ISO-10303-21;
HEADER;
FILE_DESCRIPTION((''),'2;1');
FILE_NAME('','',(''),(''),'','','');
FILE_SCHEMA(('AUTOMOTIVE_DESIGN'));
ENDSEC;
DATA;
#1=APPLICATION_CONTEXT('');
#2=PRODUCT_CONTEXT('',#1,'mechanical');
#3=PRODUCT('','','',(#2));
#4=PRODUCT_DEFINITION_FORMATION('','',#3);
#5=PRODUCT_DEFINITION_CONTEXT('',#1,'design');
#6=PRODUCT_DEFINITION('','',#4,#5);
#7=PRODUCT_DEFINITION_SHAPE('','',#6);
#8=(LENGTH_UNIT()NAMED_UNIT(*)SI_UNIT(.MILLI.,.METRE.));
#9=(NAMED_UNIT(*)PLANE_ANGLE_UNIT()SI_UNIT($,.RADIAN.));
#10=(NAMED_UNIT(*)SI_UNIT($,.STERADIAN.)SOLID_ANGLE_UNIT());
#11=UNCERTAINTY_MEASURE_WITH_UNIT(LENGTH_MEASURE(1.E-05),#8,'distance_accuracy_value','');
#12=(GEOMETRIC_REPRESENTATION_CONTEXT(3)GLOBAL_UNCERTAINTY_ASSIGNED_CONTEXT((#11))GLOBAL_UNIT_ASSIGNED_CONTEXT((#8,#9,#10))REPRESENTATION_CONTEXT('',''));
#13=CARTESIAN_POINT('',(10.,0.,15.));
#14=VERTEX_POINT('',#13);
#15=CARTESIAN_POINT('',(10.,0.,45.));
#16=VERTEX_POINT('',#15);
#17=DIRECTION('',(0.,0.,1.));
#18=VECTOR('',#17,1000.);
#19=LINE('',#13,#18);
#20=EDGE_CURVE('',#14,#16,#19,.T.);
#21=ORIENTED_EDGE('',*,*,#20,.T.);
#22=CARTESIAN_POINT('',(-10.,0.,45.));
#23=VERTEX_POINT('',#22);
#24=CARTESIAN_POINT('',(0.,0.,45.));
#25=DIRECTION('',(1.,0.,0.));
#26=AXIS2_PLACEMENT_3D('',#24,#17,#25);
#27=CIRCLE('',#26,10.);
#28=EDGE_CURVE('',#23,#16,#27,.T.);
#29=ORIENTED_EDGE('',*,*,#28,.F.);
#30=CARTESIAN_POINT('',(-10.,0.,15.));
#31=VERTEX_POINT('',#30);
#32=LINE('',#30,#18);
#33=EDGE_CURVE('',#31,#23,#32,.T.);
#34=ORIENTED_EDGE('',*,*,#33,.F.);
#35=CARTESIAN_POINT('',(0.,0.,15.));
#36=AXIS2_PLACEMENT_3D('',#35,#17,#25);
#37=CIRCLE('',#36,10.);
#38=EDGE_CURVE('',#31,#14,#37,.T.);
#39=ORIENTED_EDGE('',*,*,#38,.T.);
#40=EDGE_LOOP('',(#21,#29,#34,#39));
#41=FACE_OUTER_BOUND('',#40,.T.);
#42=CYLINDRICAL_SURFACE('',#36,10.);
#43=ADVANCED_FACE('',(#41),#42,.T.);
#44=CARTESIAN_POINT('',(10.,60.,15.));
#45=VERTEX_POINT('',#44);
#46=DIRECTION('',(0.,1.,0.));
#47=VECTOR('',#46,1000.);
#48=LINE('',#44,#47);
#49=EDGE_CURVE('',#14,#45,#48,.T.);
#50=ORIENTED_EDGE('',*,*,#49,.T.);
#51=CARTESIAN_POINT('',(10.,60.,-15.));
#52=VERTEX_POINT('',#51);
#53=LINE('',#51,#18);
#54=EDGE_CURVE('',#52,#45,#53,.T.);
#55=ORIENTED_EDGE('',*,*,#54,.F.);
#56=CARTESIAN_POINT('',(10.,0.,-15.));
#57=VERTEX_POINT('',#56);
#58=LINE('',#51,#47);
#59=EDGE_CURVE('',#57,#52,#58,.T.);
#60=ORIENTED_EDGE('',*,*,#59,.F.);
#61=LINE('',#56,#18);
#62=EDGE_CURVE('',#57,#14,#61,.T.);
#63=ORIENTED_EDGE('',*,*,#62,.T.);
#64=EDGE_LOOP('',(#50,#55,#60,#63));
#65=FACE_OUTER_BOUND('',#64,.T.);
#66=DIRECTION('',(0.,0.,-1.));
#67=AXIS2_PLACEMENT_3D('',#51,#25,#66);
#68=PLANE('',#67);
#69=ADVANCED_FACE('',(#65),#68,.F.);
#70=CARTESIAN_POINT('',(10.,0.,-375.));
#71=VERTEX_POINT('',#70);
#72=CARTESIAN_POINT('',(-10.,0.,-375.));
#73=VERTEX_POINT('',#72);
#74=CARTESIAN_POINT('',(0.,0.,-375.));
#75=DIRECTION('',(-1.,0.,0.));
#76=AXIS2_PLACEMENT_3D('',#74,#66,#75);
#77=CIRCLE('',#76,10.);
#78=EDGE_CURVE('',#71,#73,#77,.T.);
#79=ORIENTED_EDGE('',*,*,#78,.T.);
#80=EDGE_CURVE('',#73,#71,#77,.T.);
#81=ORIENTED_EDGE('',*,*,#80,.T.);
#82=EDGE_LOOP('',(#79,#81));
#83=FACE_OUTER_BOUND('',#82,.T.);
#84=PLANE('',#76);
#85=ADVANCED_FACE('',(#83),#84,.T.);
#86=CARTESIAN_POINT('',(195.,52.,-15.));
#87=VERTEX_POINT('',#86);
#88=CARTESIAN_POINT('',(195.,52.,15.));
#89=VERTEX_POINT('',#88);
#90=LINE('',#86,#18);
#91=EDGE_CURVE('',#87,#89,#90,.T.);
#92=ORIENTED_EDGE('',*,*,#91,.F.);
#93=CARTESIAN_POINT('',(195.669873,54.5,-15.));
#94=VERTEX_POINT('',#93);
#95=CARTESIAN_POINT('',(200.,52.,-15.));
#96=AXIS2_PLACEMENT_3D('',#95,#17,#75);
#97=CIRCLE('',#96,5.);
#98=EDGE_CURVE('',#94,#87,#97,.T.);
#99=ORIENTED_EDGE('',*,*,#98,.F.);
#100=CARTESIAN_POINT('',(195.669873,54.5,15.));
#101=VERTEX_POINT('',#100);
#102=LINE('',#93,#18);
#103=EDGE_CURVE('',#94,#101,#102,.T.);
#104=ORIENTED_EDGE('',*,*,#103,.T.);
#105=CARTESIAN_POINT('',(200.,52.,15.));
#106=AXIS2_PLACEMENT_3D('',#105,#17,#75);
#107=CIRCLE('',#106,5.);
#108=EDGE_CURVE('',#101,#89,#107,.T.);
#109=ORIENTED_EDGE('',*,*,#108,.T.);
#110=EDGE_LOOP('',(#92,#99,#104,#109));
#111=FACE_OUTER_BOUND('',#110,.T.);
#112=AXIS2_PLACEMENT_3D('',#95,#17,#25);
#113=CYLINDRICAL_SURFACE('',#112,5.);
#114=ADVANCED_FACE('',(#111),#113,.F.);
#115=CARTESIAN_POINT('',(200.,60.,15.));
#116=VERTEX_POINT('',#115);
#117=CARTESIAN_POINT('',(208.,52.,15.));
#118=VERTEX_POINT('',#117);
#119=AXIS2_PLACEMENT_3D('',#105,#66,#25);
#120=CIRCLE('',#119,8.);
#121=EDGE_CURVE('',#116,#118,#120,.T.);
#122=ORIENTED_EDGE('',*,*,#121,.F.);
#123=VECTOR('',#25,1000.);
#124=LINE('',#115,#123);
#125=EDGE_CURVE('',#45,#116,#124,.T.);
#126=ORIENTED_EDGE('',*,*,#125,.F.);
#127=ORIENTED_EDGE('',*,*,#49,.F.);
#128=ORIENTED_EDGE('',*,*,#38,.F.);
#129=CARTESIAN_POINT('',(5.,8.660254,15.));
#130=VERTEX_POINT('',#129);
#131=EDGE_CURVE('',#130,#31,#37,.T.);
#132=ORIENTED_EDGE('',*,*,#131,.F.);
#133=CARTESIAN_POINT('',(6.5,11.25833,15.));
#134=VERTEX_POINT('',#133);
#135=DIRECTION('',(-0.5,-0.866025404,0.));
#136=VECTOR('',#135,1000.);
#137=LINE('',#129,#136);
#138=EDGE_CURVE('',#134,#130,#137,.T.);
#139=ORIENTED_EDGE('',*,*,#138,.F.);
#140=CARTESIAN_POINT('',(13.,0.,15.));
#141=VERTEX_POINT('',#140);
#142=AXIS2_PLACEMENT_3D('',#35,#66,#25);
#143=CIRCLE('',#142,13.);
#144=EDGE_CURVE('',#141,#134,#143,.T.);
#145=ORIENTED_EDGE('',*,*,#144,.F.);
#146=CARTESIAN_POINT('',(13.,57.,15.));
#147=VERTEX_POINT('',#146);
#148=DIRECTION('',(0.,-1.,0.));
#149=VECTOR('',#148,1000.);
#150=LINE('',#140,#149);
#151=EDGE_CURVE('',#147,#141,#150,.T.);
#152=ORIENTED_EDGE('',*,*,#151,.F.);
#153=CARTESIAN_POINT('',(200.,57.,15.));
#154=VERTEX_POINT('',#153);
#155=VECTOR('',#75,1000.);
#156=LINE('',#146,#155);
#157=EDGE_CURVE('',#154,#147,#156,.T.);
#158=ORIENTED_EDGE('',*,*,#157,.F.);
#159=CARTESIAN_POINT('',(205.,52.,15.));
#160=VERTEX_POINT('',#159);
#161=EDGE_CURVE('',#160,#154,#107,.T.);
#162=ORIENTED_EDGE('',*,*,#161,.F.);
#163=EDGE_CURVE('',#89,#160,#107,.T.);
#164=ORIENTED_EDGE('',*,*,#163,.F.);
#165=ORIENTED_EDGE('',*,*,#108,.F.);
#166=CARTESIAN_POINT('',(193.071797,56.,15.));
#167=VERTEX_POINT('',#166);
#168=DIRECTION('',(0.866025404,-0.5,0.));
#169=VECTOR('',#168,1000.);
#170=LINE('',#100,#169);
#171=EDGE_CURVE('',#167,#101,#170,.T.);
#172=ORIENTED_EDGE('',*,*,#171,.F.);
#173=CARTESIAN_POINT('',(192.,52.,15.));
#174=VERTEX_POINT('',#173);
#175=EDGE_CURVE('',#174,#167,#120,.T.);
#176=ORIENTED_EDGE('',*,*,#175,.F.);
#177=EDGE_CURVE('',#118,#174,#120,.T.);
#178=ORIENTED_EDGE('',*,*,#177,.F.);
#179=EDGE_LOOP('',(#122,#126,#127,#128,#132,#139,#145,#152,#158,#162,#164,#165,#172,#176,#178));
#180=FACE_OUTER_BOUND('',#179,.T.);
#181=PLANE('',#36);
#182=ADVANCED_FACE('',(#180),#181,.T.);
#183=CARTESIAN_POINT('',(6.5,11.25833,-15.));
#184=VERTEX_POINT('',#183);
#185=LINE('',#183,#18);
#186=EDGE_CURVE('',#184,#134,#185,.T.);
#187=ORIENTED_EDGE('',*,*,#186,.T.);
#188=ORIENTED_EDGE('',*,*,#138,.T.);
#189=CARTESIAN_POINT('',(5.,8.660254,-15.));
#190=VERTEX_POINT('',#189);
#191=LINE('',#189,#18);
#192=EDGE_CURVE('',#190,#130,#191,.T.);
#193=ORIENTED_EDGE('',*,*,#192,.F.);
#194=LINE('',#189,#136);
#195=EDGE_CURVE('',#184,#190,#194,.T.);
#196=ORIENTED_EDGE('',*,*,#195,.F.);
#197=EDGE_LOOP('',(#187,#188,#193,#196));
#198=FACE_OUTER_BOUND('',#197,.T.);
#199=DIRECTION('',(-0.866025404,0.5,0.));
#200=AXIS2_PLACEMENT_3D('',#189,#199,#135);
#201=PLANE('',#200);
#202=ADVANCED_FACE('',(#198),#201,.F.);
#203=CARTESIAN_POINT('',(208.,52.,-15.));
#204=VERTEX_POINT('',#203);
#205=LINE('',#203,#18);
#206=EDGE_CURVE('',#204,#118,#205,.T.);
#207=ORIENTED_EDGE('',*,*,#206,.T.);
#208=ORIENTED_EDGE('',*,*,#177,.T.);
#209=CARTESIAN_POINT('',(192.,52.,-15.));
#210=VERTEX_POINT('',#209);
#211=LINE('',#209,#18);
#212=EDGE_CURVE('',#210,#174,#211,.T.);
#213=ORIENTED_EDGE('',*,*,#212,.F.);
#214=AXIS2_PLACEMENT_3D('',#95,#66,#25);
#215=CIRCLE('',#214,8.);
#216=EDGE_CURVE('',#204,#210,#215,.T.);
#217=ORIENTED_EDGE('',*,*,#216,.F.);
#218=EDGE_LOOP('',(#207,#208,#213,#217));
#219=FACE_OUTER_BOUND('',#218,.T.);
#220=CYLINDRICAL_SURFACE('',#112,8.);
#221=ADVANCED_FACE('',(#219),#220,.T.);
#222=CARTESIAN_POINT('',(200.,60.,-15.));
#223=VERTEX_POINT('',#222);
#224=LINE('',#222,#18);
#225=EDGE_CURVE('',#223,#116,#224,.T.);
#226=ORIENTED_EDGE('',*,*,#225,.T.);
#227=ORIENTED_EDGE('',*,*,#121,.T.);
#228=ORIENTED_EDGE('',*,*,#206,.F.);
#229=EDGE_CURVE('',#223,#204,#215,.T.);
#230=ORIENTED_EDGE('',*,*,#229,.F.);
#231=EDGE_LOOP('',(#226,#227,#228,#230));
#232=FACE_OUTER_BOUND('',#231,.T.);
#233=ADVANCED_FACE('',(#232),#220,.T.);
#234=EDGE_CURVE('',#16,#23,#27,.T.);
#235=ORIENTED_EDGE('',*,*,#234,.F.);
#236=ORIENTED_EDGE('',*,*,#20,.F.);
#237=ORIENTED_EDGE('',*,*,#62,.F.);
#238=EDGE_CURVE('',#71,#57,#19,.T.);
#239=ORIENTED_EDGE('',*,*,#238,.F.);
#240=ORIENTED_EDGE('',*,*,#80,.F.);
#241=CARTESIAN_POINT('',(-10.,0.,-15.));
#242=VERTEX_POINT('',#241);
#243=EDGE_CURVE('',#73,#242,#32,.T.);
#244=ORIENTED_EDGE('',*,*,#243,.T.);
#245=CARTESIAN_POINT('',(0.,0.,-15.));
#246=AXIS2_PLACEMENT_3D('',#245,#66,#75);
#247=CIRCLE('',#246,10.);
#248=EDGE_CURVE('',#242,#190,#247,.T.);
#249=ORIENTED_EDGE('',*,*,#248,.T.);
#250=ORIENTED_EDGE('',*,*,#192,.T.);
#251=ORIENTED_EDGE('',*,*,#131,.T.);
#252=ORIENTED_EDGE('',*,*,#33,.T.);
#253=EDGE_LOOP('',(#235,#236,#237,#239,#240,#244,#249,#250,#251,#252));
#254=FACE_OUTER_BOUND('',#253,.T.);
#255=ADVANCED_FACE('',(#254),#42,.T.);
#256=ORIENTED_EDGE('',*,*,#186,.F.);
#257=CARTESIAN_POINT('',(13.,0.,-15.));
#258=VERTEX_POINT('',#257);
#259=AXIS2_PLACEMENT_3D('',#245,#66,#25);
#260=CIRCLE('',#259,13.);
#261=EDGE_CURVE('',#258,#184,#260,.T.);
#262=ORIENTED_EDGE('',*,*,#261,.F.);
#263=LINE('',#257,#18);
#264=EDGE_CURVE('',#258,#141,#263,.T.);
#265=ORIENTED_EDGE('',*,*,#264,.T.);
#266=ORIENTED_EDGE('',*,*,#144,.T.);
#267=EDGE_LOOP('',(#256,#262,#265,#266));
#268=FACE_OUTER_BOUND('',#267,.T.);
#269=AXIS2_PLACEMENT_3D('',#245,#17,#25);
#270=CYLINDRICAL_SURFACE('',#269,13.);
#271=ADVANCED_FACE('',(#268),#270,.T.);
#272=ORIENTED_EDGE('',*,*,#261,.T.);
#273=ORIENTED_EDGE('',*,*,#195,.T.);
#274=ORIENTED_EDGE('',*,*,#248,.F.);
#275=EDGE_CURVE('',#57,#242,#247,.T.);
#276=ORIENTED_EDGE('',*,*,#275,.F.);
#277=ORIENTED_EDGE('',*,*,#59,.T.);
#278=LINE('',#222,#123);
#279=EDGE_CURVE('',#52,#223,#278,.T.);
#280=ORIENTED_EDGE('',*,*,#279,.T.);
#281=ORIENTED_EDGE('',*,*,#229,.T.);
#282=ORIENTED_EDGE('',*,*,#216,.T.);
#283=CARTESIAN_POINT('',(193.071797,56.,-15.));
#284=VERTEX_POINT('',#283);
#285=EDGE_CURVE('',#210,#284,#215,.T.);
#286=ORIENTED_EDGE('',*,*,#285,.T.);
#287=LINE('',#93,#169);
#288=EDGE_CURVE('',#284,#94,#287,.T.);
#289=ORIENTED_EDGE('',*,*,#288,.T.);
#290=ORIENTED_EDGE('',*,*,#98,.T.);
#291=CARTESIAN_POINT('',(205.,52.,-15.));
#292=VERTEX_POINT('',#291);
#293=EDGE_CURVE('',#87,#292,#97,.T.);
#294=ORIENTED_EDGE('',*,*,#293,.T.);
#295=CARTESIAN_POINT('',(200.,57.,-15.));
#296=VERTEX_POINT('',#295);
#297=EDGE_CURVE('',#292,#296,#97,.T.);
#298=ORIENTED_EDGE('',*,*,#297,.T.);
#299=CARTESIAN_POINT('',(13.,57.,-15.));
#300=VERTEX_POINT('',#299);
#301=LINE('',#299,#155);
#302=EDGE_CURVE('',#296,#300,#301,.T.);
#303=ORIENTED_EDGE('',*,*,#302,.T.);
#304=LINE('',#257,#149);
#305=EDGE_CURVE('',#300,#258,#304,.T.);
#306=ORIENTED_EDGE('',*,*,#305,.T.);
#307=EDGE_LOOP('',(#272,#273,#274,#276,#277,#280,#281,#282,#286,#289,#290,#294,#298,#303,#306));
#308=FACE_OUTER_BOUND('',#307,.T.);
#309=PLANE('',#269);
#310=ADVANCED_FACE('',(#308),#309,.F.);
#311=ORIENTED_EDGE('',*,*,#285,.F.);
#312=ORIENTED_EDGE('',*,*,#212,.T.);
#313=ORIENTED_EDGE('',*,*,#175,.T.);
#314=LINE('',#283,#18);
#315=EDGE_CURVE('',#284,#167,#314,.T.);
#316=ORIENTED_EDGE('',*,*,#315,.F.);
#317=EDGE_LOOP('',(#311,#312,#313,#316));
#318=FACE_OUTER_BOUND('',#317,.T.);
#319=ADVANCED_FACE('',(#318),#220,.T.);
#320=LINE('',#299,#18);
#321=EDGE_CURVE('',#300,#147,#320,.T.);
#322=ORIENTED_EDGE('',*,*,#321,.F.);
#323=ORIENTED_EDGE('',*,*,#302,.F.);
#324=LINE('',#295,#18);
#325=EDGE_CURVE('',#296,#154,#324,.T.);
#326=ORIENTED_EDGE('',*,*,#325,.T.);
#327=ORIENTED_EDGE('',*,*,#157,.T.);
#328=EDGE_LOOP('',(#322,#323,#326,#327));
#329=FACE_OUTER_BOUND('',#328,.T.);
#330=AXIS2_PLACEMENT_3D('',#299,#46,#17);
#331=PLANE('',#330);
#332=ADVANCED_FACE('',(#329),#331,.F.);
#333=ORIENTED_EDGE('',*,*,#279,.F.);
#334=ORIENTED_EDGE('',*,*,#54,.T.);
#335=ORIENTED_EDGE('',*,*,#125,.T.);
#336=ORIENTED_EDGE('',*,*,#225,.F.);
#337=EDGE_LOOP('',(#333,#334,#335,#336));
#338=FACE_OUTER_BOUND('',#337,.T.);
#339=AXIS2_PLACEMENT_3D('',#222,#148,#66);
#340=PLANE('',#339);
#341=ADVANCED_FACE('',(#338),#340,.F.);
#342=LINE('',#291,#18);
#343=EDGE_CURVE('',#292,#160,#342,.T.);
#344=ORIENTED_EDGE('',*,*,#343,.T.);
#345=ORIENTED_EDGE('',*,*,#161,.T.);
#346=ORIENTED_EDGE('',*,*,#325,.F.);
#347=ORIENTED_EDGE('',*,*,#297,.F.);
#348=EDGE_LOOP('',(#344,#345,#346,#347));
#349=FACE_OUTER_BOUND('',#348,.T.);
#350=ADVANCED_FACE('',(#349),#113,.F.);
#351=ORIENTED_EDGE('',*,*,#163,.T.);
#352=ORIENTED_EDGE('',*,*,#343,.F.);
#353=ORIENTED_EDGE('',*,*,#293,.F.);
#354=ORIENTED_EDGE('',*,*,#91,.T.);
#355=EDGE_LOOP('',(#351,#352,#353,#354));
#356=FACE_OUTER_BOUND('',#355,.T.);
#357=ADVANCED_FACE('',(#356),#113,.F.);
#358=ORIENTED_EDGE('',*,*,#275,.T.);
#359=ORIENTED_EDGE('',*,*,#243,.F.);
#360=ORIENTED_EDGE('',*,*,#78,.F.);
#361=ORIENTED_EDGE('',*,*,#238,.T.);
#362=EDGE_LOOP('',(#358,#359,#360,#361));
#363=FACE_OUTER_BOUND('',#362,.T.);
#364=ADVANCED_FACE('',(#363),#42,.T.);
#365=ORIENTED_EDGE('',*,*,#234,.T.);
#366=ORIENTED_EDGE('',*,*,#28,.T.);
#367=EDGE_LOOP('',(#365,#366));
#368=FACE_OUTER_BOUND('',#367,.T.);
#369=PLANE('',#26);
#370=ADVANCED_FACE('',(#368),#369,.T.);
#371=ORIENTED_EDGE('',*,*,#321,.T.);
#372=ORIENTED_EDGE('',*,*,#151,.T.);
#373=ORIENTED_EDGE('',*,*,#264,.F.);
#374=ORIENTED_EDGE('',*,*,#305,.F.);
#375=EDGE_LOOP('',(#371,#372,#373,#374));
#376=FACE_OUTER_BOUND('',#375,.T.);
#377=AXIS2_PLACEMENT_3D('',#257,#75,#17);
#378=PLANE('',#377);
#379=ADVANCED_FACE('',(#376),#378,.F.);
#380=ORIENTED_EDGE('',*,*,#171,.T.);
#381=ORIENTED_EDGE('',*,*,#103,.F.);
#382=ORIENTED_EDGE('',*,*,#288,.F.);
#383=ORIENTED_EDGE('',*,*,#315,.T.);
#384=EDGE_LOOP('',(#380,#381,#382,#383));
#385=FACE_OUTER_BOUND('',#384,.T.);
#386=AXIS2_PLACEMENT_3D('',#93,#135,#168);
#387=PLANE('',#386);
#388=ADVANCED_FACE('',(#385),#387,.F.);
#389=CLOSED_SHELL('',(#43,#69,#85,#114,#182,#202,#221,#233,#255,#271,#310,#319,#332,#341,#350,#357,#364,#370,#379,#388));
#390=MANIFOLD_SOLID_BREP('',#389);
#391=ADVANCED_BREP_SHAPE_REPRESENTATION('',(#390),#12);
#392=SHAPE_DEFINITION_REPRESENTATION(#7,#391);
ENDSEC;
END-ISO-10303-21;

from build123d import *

# Parameters (mm, degrees)
SKETCH1_W           = 10
SKETCH1_H           = 30
BOSS_EXTRUDE1_START = 30
BOSS_EXTRUDE1_DEPTH = 30
BOSS_EXTRUDE2_START = 360
SKETCH3_R           = 10
BOSS_EXTRUDE2_DEPTH = 360


with BuildPart() as part:
    # Sketch1 → Revolve1 (revolve)
    with BuildSketch(Plane(origin=(0, 0, 0), x_dir=(1, 0, 0), z_dir=(0, 1, 0))):
        with Locations((5, -30)):
            Rectangle(SKETCH1_W, SKETCH1_H)
    revolve(axis=Axis((0, 0, 15), (0, 0, 1)))

    # Sketch2 → Boss-Extrude1 (add)
    with BuildSketch(Plane(origin=(0, 0, 15), x_dir=(-1, 0, 0), z_dir=(0, 0, -1)).offset(BOSS_EXTRUDE1_START)):
        with BuildLine():
            Line((-5, 8.660254038), (-6.5, 11.258330249))
            ThreePointArc((-6.5, 11.258330249), (11.258330249, -6.5), (-13, 0))
            Line((-13, 0), (-13, 57))
            Line((-13, 57), (-200, 57))
            ThreePointArc((-200, 57), (-202.5, 47.669872981), (-195.669872981, 54.5))
            Line((-195.669872981, 54.5), (-193.07179677, 56))
            ThreePointArc((-193.07179677, 56), (-204, 45.07179677), (-200, 60))
            Line((-200, 60), (-10, 60))
            Line((-10, 60), (-10, 0))
            ThreePointArc((-10, 0), (-8.660254038, 5), (-5, 8.660254038))
        make_face()
    extrude(amount=-BOSS_EXTRUDE1_DEPTH)

    # Sketch3 → Boss-Extrude2 (add)
    with BuildSketch(Plane(origin=(0, 0, -15), x_dir=(-1, 0, 0), z_dir=(0, 0, -1)).offset(BOSS_EXTRUDE2_START)):
        with Locations(Location((0, 0, 0), (0, 0, 180))):
            Circle(SKETCH3_R)
    extrude(amount=-BOSS_EXTRUDE2_DEPTH)


solid = part.part
